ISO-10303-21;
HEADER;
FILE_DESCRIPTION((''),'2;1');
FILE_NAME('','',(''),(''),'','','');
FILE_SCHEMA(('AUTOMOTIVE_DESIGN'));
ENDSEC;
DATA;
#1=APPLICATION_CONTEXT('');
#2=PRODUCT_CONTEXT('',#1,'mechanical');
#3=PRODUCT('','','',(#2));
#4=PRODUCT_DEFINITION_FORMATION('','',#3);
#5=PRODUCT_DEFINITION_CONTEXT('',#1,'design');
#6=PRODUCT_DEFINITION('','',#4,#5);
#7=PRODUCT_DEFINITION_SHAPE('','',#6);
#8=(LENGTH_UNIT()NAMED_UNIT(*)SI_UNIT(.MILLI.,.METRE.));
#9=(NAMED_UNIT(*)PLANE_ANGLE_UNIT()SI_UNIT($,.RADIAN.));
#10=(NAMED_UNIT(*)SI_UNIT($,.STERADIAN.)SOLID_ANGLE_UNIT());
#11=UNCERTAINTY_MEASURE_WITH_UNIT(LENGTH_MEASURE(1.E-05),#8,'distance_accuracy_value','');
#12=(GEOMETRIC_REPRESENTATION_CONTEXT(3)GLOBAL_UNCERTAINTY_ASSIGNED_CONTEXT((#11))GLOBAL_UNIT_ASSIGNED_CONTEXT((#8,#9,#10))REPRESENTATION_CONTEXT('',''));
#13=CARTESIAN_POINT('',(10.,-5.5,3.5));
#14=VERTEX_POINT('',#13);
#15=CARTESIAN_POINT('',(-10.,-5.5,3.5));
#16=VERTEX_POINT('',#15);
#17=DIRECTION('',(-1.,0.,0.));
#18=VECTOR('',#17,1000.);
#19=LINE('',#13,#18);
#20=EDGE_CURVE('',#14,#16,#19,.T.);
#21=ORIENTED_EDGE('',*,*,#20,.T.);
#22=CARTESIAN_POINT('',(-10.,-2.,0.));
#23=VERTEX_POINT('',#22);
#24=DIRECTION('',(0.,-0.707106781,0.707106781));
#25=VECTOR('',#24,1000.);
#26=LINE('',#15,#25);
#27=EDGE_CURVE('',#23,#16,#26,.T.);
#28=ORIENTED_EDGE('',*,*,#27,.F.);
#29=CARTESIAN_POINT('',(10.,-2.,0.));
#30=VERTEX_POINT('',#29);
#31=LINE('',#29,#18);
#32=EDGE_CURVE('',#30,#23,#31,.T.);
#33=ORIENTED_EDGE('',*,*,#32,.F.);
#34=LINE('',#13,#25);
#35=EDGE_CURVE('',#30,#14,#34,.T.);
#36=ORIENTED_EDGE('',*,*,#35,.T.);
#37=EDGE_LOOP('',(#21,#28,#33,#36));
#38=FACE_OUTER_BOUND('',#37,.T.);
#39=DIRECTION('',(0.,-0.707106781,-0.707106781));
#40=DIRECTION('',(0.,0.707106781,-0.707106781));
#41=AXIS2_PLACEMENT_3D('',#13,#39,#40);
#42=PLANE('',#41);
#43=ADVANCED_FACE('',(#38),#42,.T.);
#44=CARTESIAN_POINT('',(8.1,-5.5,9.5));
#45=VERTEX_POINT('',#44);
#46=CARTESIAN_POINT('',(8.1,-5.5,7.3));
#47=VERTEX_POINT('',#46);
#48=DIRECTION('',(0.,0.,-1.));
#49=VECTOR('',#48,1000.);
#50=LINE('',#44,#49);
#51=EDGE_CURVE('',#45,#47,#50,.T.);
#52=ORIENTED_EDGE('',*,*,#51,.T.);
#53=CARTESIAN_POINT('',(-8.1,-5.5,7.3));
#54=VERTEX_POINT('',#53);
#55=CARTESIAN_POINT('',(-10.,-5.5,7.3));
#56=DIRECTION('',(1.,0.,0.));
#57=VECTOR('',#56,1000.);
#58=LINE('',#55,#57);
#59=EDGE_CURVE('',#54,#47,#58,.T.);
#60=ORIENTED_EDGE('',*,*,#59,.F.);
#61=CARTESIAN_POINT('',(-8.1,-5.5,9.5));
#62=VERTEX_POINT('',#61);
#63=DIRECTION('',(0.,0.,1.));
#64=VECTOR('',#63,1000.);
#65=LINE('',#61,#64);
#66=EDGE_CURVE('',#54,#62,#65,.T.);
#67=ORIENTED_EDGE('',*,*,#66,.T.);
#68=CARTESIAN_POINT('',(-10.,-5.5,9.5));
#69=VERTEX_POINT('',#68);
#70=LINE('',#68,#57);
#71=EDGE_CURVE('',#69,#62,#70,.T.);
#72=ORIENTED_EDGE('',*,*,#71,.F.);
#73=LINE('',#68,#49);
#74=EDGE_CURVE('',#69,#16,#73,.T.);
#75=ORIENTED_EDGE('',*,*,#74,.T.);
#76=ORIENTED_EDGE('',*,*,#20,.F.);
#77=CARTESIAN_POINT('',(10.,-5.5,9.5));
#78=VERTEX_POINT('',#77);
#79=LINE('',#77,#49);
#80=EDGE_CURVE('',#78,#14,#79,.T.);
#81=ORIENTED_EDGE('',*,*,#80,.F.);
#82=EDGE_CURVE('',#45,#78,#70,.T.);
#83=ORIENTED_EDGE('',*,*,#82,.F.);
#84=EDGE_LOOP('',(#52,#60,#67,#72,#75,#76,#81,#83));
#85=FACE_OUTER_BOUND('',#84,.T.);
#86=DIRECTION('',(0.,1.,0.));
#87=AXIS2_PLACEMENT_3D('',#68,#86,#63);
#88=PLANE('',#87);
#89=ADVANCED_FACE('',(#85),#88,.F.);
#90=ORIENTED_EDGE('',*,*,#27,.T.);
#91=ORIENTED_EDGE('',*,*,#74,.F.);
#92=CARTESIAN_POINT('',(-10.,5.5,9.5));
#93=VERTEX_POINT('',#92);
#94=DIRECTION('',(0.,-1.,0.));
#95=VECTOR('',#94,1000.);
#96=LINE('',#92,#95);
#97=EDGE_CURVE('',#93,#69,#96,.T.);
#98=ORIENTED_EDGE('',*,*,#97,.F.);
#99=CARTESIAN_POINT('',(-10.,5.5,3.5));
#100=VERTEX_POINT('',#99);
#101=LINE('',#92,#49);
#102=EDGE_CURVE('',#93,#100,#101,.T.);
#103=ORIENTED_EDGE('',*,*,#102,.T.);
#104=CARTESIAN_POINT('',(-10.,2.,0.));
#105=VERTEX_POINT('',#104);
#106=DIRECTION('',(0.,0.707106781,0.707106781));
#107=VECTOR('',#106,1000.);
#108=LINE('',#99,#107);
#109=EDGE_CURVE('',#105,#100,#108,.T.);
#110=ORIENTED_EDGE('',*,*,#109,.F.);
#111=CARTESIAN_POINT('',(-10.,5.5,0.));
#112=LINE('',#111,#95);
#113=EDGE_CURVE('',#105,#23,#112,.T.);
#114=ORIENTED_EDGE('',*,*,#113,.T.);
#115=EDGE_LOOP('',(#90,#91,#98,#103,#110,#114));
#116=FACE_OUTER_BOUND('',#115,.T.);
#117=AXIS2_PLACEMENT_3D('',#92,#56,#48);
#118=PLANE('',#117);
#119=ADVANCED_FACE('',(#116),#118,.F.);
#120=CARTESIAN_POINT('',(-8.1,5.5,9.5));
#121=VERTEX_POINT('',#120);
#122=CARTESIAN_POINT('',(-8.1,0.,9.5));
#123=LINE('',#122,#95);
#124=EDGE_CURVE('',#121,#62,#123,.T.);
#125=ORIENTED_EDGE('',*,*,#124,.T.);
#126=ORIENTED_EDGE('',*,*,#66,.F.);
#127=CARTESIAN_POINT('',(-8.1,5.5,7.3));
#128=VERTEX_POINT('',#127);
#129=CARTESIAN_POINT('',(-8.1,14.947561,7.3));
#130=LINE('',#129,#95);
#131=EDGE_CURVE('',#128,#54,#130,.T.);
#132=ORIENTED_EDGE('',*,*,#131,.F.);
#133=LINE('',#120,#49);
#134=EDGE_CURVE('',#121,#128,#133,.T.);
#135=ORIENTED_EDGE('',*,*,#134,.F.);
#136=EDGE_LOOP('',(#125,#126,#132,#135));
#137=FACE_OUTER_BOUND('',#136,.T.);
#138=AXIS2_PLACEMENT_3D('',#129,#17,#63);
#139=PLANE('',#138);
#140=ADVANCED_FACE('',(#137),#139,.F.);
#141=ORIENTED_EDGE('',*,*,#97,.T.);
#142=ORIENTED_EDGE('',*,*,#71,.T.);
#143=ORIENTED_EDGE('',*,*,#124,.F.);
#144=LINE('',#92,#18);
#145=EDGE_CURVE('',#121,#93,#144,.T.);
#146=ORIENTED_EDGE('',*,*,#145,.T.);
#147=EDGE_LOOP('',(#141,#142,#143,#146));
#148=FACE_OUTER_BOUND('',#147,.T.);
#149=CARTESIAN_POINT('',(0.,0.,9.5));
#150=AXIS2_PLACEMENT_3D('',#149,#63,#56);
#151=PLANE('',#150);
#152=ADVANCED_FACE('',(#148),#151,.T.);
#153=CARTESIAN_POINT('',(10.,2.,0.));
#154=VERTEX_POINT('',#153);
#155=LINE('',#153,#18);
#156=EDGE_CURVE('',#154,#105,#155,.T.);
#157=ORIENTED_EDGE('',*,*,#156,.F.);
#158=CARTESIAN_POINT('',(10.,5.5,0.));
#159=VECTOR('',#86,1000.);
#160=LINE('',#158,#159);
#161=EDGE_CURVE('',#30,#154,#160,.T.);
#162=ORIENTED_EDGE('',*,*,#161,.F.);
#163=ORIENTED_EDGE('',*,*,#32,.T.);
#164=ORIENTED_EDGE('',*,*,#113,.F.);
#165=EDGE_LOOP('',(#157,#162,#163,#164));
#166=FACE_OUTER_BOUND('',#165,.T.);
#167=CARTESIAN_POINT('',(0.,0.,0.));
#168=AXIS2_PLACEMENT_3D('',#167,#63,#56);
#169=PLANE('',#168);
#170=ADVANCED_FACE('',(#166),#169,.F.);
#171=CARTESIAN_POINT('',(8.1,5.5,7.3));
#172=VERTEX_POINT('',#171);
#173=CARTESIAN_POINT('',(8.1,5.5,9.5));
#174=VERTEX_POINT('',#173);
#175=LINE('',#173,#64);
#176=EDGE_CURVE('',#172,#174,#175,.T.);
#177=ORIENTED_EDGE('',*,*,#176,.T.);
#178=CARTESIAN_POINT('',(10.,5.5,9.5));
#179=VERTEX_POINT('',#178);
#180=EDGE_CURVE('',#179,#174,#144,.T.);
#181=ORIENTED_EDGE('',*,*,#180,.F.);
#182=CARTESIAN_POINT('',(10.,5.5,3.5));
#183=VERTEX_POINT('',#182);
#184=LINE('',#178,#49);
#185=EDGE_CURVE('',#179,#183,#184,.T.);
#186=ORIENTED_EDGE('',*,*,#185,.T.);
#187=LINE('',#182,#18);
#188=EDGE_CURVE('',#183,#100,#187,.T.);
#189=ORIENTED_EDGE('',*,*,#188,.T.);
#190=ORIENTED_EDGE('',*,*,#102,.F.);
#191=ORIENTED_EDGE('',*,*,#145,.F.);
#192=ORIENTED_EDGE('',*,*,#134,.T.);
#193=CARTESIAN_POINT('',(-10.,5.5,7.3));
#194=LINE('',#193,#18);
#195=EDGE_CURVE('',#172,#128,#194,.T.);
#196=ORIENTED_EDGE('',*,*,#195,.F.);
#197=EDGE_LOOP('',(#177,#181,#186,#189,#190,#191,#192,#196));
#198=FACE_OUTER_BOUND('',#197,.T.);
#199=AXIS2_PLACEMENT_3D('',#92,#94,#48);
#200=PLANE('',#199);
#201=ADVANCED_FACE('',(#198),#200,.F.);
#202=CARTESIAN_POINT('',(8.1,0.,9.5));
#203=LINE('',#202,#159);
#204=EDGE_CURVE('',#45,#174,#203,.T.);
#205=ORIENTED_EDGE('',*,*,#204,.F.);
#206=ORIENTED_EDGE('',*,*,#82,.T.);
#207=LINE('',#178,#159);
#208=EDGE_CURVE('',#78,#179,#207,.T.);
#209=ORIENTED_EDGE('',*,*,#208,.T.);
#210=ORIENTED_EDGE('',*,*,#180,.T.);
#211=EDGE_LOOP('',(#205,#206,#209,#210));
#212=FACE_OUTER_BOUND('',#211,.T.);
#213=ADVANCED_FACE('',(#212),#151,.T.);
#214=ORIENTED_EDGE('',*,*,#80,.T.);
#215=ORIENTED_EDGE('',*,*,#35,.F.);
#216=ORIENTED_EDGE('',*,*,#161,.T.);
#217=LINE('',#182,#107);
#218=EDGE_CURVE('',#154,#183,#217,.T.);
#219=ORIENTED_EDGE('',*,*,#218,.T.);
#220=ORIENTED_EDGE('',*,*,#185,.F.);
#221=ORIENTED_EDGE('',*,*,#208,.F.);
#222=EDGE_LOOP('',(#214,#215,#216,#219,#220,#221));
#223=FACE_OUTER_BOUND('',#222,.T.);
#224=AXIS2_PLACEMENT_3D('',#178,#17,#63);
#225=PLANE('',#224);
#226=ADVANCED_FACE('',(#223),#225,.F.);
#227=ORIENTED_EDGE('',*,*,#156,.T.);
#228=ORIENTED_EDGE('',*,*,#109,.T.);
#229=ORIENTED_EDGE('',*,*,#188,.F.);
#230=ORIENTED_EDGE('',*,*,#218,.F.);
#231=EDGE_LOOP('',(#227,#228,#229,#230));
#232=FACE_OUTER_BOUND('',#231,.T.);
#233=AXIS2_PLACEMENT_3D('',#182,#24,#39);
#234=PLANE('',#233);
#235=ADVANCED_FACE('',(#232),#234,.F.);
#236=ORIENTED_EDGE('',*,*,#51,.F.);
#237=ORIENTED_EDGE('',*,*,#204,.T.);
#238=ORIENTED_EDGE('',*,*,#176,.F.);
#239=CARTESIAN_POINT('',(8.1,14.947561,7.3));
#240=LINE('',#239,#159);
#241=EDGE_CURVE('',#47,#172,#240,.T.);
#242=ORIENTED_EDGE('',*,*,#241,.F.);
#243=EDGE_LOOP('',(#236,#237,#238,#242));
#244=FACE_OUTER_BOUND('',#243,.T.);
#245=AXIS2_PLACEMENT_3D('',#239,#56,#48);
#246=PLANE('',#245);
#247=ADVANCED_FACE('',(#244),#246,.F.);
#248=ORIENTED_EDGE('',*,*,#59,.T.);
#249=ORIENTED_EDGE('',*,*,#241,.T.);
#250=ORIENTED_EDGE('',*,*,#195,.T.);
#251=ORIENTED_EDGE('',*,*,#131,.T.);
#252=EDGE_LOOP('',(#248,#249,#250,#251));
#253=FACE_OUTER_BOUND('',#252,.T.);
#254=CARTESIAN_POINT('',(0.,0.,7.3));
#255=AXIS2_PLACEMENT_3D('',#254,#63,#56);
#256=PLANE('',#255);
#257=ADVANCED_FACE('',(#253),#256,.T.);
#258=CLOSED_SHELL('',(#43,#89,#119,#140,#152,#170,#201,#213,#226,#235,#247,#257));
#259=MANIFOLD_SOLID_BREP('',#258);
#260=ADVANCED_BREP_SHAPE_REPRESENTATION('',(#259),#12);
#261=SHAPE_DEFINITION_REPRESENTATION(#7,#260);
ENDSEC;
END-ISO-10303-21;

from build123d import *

# Parameters (mm, degrees)
SKETCH_1_W          = 20
SKETCH_1_H          = 11
EXTRUDE_1_DEPTH     = 9.5
SKETCH_2_W          = 16.2
SKETCH_2_H          = 29.89512134
CUT_EXTRUDE_1_DEPTH = 2.2
CUT_EXTRUDE_2_DEPTH = 23.814469093


with BuildPart() as part:
    # 草图1 → 凸台-拉伸1 (new body)
    with BuildSketch(Plane.XY):
        Rectangle(SKETCH_1_W, SKETCH_1_H)
    extrude(amount=EXTRUDE_1_DEPTH)

    # 草图2 → 切除-拉伸1 (cut)
    with BuildSketch(Plane.XY.offset(9.5)):
        Rectangle(SKETCH_2_W, SKETCH_2_H)
    extrude(amount=-CUT_EXTRUDE_1_DEPTH, mode=Mode.SUBTRACT)

    # 草图3 → 切除-拉伸2 (cut, through all)
    with BuildSketch(Plane.ZY.offset(10)):
        Polygon((0, 5.5), (3.5, 5.5), (0, 2), align=None)
    cut_extrude_2 = extrude(amount=-CUT_EXTRUDE_2_DEPTH, mode=Mode.SUBTRACT)

    # 镜向1: 切除-拉伸2 across plane
    add(cut_extrude_2.mirror(Plane.ZX), mode=Mode.SUBTRACT)


solid = part.part
